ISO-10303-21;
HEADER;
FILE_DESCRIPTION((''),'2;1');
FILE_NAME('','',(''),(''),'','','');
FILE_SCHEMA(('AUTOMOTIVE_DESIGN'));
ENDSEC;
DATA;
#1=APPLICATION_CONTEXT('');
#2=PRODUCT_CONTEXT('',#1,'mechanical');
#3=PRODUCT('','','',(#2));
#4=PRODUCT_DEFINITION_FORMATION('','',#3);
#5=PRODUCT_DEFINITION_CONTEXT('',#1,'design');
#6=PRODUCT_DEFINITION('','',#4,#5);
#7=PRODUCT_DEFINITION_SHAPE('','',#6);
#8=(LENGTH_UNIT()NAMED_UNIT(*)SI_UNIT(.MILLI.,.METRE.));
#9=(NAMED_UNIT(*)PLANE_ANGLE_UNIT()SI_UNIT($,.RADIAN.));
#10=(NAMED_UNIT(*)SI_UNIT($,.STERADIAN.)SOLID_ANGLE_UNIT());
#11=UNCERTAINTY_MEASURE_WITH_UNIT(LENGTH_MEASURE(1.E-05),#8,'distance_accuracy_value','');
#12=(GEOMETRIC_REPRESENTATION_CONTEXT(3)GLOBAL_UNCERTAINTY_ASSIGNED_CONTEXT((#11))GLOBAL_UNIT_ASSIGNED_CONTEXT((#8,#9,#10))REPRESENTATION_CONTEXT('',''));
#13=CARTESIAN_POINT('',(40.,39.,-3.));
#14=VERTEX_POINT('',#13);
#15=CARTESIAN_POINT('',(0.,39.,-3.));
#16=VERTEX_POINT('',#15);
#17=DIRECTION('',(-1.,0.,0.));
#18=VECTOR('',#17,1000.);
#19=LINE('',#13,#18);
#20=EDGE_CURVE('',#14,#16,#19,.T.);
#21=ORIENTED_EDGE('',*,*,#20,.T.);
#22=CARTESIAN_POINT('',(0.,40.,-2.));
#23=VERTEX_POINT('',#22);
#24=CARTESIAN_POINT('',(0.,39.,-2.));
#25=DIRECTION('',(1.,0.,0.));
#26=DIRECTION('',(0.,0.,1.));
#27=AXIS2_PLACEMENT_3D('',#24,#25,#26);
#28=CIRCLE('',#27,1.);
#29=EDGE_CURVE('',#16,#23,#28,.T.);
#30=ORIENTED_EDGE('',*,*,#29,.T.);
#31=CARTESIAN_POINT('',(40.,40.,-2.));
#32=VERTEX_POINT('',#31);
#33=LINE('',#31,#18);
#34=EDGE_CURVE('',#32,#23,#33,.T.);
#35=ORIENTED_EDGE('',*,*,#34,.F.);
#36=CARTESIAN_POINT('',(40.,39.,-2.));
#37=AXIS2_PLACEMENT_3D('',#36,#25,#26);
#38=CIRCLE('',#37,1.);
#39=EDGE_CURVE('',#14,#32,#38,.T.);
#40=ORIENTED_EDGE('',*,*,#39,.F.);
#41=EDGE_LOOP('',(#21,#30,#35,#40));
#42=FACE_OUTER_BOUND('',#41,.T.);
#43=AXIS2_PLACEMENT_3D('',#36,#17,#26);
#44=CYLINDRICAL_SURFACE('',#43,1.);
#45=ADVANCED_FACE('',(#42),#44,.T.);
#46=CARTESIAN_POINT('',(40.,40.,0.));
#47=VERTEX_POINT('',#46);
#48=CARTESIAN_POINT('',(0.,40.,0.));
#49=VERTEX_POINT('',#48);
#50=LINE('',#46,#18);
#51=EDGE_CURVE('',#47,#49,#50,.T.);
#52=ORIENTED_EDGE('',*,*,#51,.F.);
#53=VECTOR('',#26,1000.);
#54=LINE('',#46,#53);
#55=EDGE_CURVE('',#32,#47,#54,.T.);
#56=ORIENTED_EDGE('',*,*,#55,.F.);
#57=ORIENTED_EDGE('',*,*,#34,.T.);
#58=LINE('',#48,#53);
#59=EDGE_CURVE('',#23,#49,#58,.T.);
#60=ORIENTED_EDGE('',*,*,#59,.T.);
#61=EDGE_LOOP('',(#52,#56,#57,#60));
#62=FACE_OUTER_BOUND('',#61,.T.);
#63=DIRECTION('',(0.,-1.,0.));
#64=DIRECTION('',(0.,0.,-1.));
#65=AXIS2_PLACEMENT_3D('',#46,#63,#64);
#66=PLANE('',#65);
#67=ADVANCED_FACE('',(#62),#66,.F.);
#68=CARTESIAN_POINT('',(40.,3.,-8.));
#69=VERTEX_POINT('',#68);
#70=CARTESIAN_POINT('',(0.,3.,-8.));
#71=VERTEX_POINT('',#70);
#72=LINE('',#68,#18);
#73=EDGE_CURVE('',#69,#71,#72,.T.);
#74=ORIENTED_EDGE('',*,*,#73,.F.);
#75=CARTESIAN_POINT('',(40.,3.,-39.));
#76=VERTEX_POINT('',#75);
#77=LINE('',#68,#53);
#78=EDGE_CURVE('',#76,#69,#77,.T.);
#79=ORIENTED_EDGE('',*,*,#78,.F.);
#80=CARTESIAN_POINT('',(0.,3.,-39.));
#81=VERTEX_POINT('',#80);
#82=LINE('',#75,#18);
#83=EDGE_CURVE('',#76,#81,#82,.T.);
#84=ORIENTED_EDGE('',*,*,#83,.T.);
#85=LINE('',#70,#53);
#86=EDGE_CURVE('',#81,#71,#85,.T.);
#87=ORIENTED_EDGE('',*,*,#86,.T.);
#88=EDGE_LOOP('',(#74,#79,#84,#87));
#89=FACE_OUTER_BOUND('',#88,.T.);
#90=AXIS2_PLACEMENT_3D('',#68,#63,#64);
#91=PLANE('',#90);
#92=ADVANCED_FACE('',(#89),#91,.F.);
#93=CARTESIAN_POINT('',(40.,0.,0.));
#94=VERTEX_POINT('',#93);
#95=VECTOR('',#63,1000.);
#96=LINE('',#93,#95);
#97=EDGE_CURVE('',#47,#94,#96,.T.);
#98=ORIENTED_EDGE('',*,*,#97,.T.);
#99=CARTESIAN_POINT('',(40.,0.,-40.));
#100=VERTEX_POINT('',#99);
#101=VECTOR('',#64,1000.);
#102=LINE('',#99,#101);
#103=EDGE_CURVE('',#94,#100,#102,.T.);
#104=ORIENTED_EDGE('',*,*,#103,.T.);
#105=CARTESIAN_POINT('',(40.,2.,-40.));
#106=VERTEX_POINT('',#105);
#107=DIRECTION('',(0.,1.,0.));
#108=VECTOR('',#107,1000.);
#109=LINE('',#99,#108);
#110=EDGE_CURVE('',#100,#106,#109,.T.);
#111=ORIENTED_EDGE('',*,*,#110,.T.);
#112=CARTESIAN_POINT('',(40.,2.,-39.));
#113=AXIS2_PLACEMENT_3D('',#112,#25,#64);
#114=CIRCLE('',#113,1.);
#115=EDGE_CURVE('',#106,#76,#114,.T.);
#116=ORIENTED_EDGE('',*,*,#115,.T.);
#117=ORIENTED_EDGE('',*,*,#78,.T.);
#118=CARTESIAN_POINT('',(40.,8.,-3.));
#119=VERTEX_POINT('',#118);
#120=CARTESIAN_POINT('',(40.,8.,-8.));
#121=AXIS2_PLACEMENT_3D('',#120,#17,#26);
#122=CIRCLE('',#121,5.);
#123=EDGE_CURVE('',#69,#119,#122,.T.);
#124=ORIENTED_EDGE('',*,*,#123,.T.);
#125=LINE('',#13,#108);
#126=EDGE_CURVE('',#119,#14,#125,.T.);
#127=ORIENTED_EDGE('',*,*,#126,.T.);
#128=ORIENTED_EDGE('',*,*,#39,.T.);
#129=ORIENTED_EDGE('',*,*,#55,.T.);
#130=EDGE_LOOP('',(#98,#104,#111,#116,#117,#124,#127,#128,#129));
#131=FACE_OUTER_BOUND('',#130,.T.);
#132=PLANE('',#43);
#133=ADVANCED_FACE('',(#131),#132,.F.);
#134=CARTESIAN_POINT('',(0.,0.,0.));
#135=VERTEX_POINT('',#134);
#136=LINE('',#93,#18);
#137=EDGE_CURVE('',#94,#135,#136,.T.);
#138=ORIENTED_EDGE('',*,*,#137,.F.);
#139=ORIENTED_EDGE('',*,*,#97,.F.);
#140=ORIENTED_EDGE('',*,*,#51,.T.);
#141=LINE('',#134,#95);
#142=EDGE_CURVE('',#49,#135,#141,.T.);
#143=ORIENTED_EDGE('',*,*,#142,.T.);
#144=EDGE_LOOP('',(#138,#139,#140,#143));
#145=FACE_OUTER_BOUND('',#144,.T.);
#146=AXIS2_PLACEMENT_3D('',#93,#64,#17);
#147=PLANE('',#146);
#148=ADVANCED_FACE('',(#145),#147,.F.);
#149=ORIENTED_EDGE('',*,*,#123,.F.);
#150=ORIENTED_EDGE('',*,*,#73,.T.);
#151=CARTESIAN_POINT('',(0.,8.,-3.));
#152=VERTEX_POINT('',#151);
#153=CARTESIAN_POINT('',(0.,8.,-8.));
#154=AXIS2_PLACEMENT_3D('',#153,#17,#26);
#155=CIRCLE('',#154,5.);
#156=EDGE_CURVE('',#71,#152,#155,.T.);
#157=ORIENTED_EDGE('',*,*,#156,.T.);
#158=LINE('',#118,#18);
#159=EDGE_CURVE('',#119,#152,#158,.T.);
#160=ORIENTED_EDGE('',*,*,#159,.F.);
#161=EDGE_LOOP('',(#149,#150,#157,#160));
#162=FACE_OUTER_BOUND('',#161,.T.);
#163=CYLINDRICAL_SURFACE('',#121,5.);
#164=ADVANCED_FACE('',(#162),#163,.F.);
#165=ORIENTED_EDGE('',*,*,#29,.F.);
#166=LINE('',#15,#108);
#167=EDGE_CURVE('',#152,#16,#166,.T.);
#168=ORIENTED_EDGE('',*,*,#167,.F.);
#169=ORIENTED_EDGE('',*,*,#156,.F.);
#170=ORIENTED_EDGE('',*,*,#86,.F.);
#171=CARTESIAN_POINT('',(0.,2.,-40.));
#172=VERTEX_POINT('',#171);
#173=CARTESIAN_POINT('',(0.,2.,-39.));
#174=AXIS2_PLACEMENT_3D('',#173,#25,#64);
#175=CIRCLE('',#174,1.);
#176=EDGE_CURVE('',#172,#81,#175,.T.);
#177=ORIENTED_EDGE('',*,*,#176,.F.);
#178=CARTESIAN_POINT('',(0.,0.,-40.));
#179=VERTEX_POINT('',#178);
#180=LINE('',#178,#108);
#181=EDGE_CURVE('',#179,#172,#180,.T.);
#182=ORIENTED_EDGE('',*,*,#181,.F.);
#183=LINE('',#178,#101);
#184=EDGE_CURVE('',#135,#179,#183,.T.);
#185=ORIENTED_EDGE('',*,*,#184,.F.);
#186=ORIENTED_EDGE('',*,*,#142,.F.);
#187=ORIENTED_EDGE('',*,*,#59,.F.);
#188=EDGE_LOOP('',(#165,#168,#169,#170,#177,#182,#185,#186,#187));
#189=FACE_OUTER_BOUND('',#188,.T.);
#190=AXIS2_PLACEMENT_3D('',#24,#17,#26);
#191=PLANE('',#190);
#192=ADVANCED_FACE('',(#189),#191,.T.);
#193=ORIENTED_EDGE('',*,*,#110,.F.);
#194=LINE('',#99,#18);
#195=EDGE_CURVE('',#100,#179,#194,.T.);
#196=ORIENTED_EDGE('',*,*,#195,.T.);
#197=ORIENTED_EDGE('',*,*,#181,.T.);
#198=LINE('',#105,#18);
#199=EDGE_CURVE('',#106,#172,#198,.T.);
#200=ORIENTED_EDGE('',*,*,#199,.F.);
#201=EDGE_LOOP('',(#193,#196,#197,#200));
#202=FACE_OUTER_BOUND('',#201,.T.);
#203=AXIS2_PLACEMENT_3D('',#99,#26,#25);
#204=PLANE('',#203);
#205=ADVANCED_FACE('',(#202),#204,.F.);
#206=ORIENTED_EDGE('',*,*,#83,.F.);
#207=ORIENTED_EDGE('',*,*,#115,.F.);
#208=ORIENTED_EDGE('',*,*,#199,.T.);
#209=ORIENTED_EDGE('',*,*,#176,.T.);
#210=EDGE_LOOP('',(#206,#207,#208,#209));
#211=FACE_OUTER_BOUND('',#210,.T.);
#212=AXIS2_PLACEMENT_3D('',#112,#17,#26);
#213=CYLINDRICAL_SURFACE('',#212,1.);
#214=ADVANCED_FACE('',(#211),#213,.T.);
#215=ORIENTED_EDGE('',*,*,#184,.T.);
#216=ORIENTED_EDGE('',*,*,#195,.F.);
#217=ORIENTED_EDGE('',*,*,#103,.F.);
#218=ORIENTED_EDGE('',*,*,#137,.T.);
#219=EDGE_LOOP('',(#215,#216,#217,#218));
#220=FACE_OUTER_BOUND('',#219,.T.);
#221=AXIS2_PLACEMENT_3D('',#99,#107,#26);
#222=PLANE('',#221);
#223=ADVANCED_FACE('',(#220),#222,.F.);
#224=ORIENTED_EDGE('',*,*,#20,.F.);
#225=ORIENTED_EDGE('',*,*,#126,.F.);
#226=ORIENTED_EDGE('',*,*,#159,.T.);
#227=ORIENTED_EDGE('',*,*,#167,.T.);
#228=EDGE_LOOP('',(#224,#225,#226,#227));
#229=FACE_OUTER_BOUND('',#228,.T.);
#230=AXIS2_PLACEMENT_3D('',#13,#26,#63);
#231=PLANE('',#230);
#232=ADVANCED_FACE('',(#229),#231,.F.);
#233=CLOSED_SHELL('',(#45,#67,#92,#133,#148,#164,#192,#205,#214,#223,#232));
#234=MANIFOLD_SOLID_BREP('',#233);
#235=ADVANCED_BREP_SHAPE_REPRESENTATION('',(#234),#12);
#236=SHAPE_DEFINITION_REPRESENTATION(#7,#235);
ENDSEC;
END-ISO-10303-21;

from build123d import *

# Parameters (mm, degrees)
MEMBER_40_X_3_1_DEPTH = 40


with BuildPart() as part:
    # Sketch1 → Member 40 X 3_1 (new body)
    with BuildSketch(Plane(origin=(0, 0, 0), x_dir=(0, 0, -1), z_dir=(1, 0, 0))):
        with BuildLine():
            Line((0, 0), (0, 40))
            Line((0, 40), (2, 40))
            ThreePointArc((2, 40), (2.707106781, 39.707106781), (3, 39))
            Line((3, 39), (3, 8))
            ThreePointArc((3, 8), (4.464466094, 4.464466094), (8, 3))
            Line((8, 3), (39, 3))
            ThreePointArc((39, 3), (39.707106781, 2.707106781), (40, 2))
            Line((40, 2), (40, 0))
            Line((40, 0), (0, 0))
        make_face()
    extrude(amount=MEMBER_40_X_3_1_DEPTH)


solid = part.part
